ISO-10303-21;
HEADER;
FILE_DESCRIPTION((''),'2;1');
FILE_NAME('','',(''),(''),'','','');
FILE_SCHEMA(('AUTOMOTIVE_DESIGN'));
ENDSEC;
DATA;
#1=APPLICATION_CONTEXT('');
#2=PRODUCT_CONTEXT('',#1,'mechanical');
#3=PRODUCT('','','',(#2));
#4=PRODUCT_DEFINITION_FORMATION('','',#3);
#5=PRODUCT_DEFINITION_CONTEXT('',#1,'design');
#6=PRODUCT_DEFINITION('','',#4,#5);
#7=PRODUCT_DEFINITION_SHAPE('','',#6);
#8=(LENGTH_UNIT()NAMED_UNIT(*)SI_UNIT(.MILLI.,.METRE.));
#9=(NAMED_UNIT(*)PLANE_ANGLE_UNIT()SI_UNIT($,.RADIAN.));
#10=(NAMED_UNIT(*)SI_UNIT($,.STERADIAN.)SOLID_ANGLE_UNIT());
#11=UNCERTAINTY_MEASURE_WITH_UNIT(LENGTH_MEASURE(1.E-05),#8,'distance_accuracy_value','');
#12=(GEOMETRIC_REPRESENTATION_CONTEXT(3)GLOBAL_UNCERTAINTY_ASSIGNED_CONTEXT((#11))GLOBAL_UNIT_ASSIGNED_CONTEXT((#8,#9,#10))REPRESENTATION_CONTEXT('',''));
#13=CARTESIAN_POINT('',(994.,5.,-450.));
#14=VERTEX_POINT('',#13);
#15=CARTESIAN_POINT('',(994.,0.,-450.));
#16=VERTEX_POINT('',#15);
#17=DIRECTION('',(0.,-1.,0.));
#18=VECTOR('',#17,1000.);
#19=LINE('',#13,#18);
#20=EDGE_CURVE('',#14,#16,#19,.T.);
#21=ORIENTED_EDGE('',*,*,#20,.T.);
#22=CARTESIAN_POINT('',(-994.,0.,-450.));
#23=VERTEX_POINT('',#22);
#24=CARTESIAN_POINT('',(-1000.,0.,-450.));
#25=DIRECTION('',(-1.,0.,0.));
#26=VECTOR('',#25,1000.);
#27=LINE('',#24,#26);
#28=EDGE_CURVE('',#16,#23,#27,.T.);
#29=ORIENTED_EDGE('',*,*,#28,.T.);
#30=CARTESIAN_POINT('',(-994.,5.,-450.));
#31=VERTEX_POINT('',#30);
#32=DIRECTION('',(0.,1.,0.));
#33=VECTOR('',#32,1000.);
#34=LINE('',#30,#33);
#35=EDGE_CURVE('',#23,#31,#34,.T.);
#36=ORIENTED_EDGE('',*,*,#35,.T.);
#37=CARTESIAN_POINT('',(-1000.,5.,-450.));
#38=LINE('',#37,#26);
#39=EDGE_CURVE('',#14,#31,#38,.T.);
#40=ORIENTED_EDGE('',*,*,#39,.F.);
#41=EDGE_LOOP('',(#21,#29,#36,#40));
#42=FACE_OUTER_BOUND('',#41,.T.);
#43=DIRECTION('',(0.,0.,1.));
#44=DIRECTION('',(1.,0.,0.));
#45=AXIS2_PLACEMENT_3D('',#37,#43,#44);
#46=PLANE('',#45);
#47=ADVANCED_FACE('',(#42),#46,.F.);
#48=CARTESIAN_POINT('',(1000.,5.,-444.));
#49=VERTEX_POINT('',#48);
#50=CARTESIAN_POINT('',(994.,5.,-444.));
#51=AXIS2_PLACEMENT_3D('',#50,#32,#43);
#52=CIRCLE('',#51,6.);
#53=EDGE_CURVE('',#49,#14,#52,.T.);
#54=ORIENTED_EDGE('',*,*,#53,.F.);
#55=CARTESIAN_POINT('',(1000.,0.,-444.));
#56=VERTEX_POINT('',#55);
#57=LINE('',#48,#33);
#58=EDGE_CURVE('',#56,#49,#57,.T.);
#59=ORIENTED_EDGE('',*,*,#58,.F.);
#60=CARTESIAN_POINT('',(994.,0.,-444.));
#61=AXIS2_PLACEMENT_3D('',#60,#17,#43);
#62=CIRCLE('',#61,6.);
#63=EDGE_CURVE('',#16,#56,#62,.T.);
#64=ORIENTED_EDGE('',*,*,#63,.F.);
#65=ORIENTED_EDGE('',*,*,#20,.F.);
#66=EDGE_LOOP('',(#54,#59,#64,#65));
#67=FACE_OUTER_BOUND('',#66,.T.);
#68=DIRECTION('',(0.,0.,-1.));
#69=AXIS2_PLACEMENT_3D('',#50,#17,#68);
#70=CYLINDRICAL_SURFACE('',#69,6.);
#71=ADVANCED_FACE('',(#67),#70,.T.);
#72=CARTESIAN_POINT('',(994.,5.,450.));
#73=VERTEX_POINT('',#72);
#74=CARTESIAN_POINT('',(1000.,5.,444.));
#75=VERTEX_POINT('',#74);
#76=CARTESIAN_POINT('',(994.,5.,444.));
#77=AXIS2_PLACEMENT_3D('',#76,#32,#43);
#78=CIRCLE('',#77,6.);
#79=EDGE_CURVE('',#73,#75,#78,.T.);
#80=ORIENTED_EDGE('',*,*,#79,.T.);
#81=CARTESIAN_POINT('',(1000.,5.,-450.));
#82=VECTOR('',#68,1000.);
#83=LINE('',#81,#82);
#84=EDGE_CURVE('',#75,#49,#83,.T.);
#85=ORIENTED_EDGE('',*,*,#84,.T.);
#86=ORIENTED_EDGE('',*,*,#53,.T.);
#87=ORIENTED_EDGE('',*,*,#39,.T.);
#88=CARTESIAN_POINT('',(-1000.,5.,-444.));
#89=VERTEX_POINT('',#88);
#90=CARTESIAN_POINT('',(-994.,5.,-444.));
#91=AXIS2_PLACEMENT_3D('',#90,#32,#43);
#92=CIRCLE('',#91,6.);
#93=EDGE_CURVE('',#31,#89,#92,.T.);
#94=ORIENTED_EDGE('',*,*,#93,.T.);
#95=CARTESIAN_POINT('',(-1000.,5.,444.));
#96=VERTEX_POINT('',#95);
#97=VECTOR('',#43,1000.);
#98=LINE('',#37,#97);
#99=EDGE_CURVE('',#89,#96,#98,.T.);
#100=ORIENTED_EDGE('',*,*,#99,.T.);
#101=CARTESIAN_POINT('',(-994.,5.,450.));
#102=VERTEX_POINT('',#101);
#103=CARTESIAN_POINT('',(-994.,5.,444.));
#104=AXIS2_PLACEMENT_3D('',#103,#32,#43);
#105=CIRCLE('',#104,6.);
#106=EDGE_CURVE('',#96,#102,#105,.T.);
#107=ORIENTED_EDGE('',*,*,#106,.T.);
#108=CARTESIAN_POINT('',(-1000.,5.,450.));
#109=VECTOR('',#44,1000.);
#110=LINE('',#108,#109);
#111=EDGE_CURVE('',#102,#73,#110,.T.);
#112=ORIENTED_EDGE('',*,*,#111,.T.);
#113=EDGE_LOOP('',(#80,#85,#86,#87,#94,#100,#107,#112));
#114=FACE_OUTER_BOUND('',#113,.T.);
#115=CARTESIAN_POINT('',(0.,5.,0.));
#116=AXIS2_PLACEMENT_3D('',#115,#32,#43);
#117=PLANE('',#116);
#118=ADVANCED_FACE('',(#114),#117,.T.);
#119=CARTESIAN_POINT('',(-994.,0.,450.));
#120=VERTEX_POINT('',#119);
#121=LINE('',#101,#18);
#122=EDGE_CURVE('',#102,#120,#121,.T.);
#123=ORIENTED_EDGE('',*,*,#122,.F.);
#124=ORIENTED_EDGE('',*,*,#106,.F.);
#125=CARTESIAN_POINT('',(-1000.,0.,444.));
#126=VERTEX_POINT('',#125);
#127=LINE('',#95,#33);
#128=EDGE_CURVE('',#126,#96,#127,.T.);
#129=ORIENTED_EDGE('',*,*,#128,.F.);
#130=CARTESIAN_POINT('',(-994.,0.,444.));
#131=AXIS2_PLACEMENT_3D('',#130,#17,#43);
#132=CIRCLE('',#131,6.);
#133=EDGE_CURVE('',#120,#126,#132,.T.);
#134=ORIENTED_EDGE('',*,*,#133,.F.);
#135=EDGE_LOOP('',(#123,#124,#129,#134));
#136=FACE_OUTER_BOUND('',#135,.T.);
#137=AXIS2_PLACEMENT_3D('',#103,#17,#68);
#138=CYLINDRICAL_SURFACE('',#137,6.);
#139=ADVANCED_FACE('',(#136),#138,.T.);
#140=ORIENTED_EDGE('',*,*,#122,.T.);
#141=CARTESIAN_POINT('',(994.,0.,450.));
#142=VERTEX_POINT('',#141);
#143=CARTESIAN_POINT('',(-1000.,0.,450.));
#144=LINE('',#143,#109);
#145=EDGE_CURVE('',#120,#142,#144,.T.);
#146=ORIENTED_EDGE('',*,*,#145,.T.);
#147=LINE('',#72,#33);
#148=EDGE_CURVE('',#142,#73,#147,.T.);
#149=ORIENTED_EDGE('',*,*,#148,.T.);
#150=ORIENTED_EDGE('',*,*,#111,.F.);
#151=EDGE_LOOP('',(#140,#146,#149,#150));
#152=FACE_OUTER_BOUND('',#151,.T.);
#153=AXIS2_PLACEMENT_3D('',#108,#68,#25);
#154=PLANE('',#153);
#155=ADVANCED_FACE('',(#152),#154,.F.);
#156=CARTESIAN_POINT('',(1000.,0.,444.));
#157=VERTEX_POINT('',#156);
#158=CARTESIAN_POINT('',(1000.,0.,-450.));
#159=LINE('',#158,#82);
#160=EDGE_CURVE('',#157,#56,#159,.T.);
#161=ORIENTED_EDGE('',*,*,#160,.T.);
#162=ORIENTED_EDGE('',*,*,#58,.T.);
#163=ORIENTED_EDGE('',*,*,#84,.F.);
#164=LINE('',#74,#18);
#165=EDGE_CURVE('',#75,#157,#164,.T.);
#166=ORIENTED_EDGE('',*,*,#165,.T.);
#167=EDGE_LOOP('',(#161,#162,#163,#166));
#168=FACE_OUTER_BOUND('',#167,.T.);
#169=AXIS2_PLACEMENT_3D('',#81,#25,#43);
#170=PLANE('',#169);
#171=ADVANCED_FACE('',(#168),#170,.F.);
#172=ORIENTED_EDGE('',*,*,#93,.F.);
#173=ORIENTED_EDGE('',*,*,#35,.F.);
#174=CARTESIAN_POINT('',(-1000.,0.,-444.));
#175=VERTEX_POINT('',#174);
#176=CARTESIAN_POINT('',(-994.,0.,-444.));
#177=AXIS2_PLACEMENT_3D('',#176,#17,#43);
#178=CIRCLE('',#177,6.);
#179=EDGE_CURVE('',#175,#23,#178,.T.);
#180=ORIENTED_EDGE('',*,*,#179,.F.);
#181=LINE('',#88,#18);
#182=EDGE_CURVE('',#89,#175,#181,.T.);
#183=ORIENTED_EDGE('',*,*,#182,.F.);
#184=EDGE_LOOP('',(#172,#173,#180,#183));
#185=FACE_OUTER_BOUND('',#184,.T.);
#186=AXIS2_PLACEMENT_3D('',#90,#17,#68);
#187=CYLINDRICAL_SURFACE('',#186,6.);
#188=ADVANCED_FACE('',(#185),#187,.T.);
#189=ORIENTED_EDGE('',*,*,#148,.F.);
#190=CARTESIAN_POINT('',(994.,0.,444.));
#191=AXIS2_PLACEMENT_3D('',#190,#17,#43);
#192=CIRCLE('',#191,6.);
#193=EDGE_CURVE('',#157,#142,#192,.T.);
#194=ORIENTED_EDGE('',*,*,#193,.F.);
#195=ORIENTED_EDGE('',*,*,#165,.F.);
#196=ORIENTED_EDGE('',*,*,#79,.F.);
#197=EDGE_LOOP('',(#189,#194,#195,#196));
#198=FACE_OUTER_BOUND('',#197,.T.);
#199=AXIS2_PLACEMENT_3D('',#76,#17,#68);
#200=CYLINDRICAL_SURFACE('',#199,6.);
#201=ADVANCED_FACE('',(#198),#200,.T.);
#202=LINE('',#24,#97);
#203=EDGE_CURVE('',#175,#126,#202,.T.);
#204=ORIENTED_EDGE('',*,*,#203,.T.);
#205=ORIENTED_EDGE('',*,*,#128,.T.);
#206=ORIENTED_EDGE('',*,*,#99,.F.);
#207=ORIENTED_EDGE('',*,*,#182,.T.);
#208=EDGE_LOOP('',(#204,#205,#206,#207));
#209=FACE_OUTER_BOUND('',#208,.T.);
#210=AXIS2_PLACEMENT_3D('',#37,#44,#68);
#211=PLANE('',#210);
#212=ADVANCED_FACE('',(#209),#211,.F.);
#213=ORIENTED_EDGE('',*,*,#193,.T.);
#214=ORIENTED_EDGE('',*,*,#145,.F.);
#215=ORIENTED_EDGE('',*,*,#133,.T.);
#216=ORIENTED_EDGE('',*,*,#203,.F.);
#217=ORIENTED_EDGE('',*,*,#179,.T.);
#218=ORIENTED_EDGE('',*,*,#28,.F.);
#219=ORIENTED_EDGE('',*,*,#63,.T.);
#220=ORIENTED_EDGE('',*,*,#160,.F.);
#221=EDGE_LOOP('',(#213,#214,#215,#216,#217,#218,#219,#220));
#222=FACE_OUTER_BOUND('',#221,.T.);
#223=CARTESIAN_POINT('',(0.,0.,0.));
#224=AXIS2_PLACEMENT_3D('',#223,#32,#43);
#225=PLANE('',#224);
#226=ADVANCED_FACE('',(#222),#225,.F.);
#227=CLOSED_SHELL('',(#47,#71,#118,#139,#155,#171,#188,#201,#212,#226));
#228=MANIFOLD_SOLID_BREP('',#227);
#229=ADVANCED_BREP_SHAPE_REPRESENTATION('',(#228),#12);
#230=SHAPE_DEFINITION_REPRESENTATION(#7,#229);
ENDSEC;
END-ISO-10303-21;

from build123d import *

# Parameters (mm, degrees)
SKETCH1_W           = 2000
SKETCH1_H           = 900
BOSS_EXTRUDE1_DEPTH = 5
FILLET1_R           = 6


with BuildPart() as part:
    # Sketch1 → Boss-Extrude1 (new body)
    with BuildSketch(Plane(origin=(0, 0, 0), x_dir=(1, 0, 0), z_dir=(0, 1, 0))):
        Rectangle(SKETCH1_W, SKETCH1_H)
    extrude(amount=BOSS_EXTRUDE1_DEPTH)

    # Fillet1
    fillet1_edges = [part.edges().sort_by_distance(p)[0] for p in [
        (1000, 2.5, 450),
        (-1000, 2.5, 450),
        (-1000, 2.5, -450),
        (1000, 2.5, -450),
    ]]
    fillet(fillet1_edges, radius=FILLET1_R)


solid = part.part
